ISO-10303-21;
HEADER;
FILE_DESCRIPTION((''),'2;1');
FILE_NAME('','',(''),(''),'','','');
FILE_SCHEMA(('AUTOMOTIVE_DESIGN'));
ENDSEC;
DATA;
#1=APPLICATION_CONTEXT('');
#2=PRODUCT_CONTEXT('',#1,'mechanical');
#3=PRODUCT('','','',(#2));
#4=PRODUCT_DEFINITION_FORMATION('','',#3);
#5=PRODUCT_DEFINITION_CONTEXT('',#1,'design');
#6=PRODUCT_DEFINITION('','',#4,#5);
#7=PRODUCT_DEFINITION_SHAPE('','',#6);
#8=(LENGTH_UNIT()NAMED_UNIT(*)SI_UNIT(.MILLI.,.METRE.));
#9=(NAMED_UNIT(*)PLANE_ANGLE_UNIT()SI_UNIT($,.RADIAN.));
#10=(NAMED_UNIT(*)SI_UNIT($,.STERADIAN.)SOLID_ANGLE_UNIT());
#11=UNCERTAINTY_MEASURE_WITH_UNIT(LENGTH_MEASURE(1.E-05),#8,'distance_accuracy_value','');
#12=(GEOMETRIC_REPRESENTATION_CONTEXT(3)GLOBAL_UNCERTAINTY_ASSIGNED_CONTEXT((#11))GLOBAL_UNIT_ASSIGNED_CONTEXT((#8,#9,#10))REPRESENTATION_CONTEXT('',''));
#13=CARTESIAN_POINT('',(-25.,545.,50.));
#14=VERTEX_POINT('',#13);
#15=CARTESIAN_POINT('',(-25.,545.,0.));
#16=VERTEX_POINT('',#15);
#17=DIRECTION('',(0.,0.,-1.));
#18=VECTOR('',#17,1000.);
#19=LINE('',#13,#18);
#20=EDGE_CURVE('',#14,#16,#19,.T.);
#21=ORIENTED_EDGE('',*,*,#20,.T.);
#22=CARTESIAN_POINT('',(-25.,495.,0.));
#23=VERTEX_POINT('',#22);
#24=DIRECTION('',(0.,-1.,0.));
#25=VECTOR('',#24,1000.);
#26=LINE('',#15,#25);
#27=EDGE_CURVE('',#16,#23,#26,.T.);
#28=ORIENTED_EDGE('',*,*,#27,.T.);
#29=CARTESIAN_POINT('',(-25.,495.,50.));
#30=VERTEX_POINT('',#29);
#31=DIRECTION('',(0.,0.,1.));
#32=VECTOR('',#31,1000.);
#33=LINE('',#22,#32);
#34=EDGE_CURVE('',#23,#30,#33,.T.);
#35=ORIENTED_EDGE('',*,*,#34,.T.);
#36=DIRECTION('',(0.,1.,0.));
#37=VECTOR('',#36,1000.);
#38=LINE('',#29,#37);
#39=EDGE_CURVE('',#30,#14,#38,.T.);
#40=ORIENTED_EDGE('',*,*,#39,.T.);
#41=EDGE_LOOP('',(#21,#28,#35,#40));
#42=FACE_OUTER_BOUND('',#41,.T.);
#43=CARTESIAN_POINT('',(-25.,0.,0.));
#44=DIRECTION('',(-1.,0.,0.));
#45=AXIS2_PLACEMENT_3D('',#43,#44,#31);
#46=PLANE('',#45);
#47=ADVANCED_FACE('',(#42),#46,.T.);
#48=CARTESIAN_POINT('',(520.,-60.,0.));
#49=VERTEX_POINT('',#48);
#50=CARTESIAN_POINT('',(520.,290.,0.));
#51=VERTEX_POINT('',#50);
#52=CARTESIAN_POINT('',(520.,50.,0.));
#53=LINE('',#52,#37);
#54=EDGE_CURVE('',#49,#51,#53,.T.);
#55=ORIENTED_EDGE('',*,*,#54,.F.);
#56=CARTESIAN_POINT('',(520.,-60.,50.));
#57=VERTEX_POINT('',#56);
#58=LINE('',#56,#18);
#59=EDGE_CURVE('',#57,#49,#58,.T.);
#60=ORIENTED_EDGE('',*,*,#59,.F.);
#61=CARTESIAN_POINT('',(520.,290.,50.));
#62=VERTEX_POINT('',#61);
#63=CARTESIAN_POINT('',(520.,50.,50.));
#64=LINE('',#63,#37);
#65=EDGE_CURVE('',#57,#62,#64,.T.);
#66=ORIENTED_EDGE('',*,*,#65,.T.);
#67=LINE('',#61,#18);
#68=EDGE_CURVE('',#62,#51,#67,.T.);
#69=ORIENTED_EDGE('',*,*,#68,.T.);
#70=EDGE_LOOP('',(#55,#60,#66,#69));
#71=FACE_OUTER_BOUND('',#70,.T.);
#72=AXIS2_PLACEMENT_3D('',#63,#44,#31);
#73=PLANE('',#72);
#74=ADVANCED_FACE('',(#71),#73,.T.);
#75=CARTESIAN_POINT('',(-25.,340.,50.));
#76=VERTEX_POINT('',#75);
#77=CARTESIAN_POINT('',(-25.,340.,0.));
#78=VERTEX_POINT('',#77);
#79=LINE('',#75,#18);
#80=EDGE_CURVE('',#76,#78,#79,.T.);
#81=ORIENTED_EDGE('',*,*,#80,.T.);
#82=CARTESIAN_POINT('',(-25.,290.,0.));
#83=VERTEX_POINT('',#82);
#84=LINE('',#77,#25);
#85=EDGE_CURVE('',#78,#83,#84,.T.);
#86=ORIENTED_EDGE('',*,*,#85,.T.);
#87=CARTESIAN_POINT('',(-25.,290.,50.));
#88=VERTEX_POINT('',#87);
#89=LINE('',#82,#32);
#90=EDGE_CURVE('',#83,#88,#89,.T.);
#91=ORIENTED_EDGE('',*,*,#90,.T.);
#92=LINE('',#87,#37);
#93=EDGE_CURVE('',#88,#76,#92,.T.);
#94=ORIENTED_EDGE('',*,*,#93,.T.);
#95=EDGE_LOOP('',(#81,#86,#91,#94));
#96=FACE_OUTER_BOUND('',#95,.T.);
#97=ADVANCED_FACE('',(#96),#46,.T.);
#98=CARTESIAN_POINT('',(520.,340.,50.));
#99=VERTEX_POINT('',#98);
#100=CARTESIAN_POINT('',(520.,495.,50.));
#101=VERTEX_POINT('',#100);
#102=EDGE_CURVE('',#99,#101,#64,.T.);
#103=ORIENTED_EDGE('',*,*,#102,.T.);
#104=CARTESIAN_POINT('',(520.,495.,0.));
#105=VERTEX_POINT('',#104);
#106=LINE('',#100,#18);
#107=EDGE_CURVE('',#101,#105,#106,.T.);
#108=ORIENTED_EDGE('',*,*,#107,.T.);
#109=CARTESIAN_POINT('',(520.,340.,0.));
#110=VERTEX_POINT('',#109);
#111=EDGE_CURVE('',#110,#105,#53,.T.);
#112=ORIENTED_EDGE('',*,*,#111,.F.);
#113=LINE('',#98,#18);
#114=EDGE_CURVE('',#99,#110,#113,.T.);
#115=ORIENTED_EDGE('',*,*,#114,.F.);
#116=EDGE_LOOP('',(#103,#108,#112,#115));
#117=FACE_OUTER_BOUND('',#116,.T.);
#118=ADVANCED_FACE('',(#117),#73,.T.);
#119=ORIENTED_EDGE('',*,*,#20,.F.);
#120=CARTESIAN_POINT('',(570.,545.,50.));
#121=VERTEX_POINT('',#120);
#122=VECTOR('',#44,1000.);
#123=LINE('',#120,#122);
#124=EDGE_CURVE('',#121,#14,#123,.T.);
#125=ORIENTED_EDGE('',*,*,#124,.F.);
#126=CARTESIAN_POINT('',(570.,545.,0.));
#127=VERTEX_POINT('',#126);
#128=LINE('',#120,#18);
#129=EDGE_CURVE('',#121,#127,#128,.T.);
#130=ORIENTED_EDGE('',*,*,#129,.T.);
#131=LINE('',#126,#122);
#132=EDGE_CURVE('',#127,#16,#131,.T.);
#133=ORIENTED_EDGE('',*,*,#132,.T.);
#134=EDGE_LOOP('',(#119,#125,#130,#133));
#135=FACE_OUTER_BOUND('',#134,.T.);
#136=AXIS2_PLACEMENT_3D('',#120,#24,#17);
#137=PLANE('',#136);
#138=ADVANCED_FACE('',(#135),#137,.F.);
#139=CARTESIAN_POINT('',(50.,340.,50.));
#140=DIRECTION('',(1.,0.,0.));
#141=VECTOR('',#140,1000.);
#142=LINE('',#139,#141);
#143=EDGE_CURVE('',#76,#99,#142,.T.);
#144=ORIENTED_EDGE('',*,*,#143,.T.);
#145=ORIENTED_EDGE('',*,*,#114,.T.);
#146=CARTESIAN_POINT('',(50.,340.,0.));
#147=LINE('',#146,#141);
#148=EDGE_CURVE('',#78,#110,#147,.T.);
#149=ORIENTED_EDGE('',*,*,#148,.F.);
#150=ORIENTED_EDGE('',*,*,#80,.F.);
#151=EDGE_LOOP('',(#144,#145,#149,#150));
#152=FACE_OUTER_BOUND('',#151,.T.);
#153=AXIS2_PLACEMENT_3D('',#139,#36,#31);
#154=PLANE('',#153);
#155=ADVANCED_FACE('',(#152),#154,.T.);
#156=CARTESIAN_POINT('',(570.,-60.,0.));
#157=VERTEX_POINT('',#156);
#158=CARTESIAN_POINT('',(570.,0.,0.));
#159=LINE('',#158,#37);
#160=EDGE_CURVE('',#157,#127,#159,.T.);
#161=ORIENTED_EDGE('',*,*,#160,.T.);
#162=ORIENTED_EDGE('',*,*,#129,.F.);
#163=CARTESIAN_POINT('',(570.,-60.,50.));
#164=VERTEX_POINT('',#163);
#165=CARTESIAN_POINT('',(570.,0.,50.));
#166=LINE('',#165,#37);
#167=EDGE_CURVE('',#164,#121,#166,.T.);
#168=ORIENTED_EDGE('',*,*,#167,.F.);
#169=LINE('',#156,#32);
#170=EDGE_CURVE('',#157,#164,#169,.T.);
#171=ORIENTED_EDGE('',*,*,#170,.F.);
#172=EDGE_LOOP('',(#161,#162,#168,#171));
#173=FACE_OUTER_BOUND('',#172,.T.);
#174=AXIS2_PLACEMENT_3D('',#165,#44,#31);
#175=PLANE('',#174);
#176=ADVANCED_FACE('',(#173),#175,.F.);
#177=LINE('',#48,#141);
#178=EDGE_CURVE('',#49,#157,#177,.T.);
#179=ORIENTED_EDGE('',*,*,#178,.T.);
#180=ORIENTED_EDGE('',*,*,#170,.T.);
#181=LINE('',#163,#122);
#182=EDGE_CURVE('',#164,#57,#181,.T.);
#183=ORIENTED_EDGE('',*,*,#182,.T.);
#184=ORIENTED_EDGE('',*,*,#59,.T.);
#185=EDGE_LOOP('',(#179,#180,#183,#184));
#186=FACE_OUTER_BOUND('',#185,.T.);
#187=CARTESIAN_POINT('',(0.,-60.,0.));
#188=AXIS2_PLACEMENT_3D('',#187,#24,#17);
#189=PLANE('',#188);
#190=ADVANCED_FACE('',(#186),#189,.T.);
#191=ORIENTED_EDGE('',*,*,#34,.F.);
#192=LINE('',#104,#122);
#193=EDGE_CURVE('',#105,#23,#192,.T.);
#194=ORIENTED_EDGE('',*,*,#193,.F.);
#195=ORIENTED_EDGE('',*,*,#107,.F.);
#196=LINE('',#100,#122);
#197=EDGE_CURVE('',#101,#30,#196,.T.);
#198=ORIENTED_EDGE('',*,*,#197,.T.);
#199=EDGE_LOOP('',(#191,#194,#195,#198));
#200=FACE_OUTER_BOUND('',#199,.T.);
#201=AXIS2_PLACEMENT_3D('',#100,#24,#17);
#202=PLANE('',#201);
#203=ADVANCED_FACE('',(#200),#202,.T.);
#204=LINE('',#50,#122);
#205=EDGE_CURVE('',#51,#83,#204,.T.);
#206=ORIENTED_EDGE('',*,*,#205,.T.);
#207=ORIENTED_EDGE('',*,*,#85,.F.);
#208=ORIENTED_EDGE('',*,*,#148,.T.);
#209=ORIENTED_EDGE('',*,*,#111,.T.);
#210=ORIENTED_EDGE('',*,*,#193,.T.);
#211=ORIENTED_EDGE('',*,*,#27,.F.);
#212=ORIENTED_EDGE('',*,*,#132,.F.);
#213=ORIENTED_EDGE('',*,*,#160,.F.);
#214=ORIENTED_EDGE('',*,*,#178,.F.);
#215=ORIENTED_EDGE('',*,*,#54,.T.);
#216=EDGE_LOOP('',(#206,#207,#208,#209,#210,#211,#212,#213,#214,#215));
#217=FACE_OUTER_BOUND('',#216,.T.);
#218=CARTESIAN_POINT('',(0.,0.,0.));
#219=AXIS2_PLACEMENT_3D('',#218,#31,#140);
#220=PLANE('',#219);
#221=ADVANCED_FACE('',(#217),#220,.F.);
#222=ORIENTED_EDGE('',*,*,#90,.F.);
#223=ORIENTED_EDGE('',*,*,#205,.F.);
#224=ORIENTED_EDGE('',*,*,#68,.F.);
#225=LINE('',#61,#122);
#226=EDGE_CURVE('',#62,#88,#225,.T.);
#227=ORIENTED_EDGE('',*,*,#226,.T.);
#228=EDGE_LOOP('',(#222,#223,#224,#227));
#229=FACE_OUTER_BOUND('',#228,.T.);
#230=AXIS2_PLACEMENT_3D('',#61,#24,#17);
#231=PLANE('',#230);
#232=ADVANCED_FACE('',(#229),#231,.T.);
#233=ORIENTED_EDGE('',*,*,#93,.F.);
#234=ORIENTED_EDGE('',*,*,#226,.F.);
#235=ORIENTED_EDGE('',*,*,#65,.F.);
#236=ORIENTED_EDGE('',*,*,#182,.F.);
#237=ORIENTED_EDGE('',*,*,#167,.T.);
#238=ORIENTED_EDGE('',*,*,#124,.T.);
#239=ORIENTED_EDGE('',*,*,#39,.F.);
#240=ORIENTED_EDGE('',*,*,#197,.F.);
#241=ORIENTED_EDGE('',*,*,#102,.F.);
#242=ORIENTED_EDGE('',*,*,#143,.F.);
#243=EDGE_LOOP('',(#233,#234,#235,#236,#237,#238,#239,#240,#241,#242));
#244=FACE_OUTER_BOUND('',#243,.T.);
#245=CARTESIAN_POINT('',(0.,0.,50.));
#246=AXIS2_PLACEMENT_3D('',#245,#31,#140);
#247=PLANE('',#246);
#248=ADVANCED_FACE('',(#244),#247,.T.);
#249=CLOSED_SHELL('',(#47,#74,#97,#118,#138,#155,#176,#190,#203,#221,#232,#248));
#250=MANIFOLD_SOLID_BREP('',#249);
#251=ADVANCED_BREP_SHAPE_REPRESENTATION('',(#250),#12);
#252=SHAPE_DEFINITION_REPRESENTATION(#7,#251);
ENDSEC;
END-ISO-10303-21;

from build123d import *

# Parameters (mm, degrees)
SKETCH_1_W          = 570
SKETCH_1_H          = 545
SKETCH_1_W_2        = 470
SKETCH_1_H_2        = 445
EXTRUDE_1_DEPTH     = 50
SKETCH_2_W          = 470
SKETCH_2_H          = 50
EXTRUDE_2_DEPTH     = 50
SKETCH_3_W          = 50
SKETCH_3_H          = 50
EXTRUDE_3_DEPTH     = 50
SKETCH_4_W          = 470
SKETCH_4_H          = 50
CUT_EXTRUDE_1_DEPTH = 50
EXTRUDE_4_DEPTH     = 478
SKETCH_6_W          = 570
SKETCH_6_H          = 50
CUT_EXTRUDE_2_DEPTH = 76
SKETCH_7_W          = 50
SKETCH_7_H          = 545
EXTRUDE_5_DEPTH     = 50
SKETCH_8_W          = 50
SKETCH_8_H          = 545
CUT_EXTRUDE_3_DEPTH = 50
SKETCH_9_W          = 50
SKETCH_9_H          = 50
EXTRUDE_6_DEPTH     = 20
SKETCH_10_W         = 50
SKETCH_10_H         = 50
EXTRUDE_7_DEPTH     = 10
SKETCH_11_W         = 50
SKETCH_11_H         = 50
EXTRUDE_8_DEPTH     = 60
SKETCH_12_W         = 50
SKETCH_12_H         = 50
EXTRUDE_9_DEPTH     = 45


with BuildPart() as part:
    # 草图1 → 凸台-拉伸1 (new body)
    with BuildSketch(Plane.XY):
        with Locations((285, 272.5)):
            Rectangle(SKETCH_1_W, SKETCH_1_H)
        with Locations((285, 272.5)):
            Rectangle(SKETCH_1_W_2, SKETCH_1_H_2, mode=Mode.SUBTRACT)
    extrude(amount=EXTRUDE_1_DEPTH)

    # 草图2 → 凸台-拉伸2 (add)
    with BuildSketch(Plane(origin=(0, 0, 0), x_dir=(-1, 0, 0), z_dir=(0, 0, -1))):
        with Locations((-285, 315)):
            Rectangle(SKETCH_2_W, SKETCH_2_H)
    extrude(amount=-EXTRUDE_2_DEPTH)

    # 草图3 → 凸台-拉伸3 (add)
    with BuildSketch(Plane.XZ):
        with Locations((25, 25)):
            Rectangle(SKETCH_3_W, SKETCH_3_H)
        with Locations((545, 25)):
            Rectangle(SKETCH_3_W, SKETCH_3_H)
    extrude(amount=EXTRUDE_3_DEPTH)

    # 草图4 → 切除-拉伸1 (cut)
    with BuildSketch(Plane.XY.offset(50)):
        with Locations((285, 25)):
            Rectangle(SKETCH_4_W, SKETCH_4_H)
    extrude(amount=-CUT_EXTRUDE_1_DEPTH, mode=Mode.SUBTRACT)

    # 草图5 → 凸台-拉伸4 (add)
    with BuildSketch(Plane.ZY.offset(-520)):
        Polygon((50, -50), (0, -50), (0, 0), (50, 0), (50, -10.325702711), align=None)
    extrude(amount=EXTRUDE_4_DEPTH)

    # 草图6 → 切除-拉伸2 (cut)
    with BuildSketch(Plane.XY.offset(50)):
        with Locations((285, -25)):
            Rectangle(SKETCH_6_W, SKETCH_6_H)
    extrude(amount=-CUT_EXTRUDE_2_DEPTH, mode=Mode.SUBTRACT)

    # 草图7 → 凸台-拉伸5 (add)
    with BuildSketch(Plane.ZY):
        with Locations((25, 272.5)):
            Rectangle(SKETCH_7_W, SKETCH_7_H)
    extrude(amount=-EXTRUDE_5_DEPTH)

    # 草图8 → 切除-拉伸3 (cut)
    with BuildSketch(Plane.ZY):
        with Locations((25, 272.5)):
            Rectangle(SKETCH_8_W, SKETCH_8_H)
    extrude(amount=-CUT_EXTRUDE_3_DEPTH, mode=Mode.SUBTRACT)

    # 草图9 → 凸台-拉伸6 (add)
    with BuildSketch(Plane.ZY.offset(-50)):
        with Locations((25, 520)):
            Rectangle(SKETCH_9_W, SKETCH_9_H)
        with Locations((25, 315)):
            Rectangle(SKETCH_9_W, SKETCH_9_H)
    extrude(amount=EXTRUDE_6_DEPTH)

    # 草图10 → 凸台-拉伸7 (add)
    with BuildSketch(Plane.ZY.offset(-30)):
        with Locations((25, 520)):
            Rectangle(SKETCH_10_W, SKETCH_10_H)
        with Locations((25, 315)):
            Rectangle(SKETCH_10_W, SKETCH_10_H)
    extrude(amount=EXTRUDE_7_DEPTH)

    # 草图11 → 凸台-拉伸8 (add)
    with BuildSketch(Plane.XZ):
        with Locations((545, 25)):
            Rectangle(SKETCH_11_W, SKETCH_11_H)
    extrude(amount=EXTRUDE_8_DEPTH)

    # 草图12 → 凸台-拉伸9 (add)
    with BuildSketch(Plane.ZY.offset(-20)):
        with Locations((25, 520)):
            Rectangle(SKETCH_12_W, SKETCH_12_H)
        with Locations((25, 315)):
            Rectangle(SKETCH_12_W, SKETCH_12_H)
    extrude(amount=EXTRUDE_9_DEPTH)


solid = part.part
